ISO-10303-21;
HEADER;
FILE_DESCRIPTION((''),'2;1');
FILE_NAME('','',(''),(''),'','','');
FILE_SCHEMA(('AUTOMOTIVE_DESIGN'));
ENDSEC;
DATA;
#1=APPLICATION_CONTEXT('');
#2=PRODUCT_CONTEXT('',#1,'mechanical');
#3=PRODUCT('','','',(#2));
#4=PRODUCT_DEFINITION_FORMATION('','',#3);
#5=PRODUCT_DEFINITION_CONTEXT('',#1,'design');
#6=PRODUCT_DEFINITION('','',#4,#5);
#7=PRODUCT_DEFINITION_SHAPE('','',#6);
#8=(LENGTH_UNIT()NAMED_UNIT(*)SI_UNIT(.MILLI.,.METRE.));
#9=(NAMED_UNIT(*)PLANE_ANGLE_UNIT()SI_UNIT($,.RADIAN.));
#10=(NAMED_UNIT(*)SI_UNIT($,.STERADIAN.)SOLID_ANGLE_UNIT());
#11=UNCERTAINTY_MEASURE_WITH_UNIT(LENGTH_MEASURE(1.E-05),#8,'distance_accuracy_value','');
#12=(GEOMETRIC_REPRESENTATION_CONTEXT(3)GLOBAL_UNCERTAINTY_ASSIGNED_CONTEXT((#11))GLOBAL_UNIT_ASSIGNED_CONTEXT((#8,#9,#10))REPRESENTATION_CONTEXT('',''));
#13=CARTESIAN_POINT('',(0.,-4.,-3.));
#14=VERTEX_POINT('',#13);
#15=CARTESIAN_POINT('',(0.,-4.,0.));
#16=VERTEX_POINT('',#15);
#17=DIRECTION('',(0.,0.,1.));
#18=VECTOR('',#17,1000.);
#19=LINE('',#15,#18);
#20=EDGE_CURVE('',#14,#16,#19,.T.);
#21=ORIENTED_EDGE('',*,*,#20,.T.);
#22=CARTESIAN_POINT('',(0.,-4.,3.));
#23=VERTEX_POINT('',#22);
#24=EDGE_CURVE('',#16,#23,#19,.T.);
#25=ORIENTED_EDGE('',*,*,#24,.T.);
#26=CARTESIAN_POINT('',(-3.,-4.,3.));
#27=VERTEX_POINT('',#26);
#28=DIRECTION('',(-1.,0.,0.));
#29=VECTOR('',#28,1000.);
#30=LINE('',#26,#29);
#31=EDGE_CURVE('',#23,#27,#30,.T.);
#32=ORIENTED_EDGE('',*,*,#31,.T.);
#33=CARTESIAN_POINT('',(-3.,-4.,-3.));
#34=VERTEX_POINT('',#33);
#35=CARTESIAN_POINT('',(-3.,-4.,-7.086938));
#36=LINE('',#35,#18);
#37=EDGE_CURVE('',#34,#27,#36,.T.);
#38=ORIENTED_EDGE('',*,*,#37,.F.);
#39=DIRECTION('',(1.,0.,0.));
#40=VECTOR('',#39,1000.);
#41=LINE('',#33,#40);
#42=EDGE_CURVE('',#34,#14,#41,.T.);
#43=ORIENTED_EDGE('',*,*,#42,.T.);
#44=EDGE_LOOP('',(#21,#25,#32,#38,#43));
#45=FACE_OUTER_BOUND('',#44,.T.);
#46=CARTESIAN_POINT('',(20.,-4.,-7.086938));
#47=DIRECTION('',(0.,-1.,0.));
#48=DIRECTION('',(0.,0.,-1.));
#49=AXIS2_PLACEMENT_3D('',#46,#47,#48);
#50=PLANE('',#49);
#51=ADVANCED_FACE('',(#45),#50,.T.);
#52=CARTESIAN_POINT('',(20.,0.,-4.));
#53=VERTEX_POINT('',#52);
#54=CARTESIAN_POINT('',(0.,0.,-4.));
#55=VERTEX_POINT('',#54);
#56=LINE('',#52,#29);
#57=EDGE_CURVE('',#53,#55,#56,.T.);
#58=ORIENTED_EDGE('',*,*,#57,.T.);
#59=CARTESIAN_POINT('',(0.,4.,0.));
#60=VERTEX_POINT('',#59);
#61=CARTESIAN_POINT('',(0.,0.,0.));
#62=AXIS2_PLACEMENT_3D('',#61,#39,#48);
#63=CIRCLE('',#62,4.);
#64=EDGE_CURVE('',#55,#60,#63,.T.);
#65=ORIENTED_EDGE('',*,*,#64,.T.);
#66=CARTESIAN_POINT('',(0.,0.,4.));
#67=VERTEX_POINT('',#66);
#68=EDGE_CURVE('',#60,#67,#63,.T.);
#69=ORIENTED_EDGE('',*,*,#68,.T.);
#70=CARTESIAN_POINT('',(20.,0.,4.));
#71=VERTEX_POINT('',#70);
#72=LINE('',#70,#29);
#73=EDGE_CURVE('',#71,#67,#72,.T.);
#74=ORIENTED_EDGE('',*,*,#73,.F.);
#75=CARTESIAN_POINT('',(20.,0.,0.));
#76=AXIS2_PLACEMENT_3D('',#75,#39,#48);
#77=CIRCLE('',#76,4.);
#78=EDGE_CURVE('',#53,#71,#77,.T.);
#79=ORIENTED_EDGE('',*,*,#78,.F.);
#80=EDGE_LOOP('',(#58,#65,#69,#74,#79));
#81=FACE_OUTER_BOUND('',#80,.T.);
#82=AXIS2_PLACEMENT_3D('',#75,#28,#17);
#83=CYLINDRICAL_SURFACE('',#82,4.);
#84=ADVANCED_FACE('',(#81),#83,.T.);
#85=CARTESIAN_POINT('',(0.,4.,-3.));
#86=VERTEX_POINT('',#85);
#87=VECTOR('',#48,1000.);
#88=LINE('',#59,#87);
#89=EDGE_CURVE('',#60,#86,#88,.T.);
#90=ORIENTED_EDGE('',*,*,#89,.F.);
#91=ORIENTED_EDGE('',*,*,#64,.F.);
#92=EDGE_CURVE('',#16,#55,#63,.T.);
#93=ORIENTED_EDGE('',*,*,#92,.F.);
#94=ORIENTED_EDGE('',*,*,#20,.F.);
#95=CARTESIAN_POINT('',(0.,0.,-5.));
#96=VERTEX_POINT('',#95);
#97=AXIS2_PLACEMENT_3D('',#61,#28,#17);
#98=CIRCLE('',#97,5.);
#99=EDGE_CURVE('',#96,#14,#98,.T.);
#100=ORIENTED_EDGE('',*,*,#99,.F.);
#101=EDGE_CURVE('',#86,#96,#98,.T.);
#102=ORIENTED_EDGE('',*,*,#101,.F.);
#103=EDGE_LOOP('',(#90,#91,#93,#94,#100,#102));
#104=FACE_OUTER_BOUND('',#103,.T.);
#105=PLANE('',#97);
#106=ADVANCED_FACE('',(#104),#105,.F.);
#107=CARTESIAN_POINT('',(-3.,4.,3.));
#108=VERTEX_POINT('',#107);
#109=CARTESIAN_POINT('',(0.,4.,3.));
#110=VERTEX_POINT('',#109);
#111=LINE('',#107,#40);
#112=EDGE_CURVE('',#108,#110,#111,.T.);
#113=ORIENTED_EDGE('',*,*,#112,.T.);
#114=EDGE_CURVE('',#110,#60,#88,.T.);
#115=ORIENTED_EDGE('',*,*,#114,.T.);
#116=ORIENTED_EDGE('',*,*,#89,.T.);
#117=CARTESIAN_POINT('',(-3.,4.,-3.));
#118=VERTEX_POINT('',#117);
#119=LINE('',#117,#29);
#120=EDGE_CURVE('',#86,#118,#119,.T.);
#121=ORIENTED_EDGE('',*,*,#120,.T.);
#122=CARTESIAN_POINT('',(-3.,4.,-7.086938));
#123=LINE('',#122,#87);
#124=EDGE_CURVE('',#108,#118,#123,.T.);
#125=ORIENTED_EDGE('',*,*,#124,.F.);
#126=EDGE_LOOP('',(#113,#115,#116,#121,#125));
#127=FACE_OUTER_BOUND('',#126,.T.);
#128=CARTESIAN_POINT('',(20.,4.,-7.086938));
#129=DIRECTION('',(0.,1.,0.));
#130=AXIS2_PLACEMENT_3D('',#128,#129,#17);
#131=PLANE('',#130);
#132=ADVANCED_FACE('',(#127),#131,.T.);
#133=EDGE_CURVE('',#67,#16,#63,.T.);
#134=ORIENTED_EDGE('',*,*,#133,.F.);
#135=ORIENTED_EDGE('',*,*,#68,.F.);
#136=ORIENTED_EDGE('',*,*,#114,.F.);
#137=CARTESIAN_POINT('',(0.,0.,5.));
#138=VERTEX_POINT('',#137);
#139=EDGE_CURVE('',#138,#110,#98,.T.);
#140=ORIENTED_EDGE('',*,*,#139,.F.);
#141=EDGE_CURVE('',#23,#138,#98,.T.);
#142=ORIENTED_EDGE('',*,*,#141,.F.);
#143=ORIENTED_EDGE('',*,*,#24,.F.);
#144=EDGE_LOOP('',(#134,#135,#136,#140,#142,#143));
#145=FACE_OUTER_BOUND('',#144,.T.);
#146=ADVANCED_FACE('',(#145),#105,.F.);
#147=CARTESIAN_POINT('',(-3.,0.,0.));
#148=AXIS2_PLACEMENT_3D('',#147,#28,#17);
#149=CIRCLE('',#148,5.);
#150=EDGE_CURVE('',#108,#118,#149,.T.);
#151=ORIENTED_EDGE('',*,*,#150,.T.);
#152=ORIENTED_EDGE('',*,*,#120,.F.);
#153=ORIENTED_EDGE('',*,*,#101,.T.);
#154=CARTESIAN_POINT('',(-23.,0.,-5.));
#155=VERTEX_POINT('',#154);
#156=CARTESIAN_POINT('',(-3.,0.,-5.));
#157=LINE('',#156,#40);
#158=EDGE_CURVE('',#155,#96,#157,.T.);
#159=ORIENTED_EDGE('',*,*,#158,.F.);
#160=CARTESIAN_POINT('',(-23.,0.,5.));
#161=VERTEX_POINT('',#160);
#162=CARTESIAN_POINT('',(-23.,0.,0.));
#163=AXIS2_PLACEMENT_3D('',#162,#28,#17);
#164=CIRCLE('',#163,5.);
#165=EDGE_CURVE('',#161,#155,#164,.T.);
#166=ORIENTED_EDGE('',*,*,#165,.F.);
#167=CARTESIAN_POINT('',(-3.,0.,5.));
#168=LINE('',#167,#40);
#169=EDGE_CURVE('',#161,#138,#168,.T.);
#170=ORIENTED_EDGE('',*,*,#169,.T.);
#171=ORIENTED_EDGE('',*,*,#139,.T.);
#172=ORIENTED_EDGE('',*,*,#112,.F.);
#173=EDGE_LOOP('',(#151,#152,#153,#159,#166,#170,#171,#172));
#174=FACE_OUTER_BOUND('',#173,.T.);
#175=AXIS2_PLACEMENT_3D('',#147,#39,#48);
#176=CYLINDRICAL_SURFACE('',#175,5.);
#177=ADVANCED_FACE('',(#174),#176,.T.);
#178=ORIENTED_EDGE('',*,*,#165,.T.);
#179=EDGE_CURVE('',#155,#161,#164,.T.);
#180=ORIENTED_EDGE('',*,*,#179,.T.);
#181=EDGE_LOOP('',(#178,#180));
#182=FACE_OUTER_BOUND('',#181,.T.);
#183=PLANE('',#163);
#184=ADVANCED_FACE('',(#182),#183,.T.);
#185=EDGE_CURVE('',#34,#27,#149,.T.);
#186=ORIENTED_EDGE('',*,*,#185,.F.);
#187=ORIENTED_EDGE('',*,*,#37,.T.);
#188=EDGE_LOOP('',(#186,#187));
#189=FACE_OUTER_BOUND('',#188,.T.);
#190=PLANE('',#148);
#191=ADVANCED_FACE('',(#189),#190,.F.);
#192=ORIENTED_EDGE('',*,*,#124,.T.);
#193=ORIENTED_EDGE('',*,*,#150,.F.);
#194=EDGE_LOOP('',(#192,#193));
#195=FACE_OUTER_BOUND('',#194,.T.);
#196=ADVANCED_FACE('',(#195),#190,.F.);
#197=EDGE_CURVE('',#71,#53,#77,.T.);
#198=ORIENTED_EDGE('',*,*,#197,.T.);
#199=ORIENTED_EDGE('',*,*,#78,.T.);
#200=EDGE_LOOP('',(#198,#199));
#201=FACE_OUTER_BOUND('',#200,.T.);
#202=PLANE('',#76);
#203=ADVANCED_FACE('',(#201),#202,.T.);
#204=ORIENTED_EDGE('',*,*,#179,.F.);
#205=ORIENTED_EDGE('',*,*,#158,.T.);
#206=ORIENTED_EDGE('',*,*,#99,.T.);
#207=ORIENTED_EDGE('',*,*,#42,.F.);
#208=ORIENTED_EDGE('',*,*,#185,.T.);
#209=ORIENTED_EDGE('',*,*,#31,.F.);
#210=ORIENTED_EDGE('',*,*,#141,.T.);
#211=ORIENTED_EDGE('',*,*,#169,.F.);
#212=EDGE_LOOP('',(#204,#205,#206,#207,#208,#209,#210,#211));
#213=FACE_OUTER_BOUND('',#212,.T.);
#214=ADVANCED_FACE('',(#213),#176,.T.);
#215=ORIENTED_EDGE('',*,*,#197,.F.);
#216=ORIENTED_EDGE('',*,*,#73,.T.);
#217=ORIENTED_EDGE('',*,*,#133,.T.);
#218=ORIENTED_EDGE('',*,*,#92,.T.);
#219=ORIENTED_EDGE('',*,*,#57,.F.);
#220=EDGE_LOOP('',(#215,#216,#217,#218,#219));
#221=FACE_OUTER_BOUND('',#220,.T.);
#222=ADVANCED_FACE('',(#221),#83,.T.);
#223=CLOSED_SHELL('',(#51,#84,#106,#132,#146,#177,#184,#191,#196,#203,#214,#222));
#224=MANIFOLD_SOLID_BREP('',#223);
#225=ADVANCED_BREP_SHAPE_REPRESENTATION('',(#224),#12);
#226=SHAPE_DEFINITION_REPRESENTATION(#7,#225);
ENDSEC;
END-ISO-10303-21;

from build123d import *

# Parameters (mm, degrees)
SKETCH_1_R           = 4
EXTRUDE_1_DEPTH      = 20
SKETCH_2_R           = 5
EXTRUDE_2_DEPTH      = 3
SKETCH_3_OUTSIDE_W   = 17.4
SKETCH_3_OUTSIDE_H   = 17.4
SKETCH_3_OUTSIDE_W_2 = 14.173876264
SKETCH_3_OUTSIDE_H_2 = 8
CUT_EXTRUDE_1_DEPTH  = 25.062418831
SKETCH_4_R           = 5
EXTRUDE_3_DEPTH      = 20


with BuildPart() as part:
    # 草图1 → 凸台-拉伸1 (new body)
    with BuildSketch(Plane(origin=(0, 0, 0), x_dir=(0, 0, -1), z_dir=(1, 0, 0))):
        Circle(SKETCH_1_R)
    extrude(amount=EXTRUDE_1_DEPTH)

    # 草图2 → 凸台-拉伸2 (add)
    with BuildSketch(Plane.ZY):
        Circle(SKETCH_2_R)
    extrude(amount=EXTRUDE_2_DEPTH)

    # 草图3 outside → 切除-拉伸1 (cut, through all)
    with BuildSketch(Plane.ZY.offset(3)):
        Rectangle(SKETCH_3_OUTSIDE_W, SKETCH_3_OUTSIDE_H)
        Rectangle(SKETCH_3_OUTSIDE_W_2, SKETCH_3_OUTSIDE_H_2, mode=Mode.SUBTRACT)
    extrude(amount=-CUT_EXTRUDE_1_DEPTH, mode=Mode.SUBTRACT)

    # 草图4 → 凸台-拉伸3 (add)
    with BuildSketch(Plane.ZY.offset(3)):
        with Locations(Location((0, 0, 0), (0, 0, 126.869897646))):
            Circle(SKETCH_4_R)
    extrude(amount=EXTRUDE_3_DEPTH)


solid = part.part
